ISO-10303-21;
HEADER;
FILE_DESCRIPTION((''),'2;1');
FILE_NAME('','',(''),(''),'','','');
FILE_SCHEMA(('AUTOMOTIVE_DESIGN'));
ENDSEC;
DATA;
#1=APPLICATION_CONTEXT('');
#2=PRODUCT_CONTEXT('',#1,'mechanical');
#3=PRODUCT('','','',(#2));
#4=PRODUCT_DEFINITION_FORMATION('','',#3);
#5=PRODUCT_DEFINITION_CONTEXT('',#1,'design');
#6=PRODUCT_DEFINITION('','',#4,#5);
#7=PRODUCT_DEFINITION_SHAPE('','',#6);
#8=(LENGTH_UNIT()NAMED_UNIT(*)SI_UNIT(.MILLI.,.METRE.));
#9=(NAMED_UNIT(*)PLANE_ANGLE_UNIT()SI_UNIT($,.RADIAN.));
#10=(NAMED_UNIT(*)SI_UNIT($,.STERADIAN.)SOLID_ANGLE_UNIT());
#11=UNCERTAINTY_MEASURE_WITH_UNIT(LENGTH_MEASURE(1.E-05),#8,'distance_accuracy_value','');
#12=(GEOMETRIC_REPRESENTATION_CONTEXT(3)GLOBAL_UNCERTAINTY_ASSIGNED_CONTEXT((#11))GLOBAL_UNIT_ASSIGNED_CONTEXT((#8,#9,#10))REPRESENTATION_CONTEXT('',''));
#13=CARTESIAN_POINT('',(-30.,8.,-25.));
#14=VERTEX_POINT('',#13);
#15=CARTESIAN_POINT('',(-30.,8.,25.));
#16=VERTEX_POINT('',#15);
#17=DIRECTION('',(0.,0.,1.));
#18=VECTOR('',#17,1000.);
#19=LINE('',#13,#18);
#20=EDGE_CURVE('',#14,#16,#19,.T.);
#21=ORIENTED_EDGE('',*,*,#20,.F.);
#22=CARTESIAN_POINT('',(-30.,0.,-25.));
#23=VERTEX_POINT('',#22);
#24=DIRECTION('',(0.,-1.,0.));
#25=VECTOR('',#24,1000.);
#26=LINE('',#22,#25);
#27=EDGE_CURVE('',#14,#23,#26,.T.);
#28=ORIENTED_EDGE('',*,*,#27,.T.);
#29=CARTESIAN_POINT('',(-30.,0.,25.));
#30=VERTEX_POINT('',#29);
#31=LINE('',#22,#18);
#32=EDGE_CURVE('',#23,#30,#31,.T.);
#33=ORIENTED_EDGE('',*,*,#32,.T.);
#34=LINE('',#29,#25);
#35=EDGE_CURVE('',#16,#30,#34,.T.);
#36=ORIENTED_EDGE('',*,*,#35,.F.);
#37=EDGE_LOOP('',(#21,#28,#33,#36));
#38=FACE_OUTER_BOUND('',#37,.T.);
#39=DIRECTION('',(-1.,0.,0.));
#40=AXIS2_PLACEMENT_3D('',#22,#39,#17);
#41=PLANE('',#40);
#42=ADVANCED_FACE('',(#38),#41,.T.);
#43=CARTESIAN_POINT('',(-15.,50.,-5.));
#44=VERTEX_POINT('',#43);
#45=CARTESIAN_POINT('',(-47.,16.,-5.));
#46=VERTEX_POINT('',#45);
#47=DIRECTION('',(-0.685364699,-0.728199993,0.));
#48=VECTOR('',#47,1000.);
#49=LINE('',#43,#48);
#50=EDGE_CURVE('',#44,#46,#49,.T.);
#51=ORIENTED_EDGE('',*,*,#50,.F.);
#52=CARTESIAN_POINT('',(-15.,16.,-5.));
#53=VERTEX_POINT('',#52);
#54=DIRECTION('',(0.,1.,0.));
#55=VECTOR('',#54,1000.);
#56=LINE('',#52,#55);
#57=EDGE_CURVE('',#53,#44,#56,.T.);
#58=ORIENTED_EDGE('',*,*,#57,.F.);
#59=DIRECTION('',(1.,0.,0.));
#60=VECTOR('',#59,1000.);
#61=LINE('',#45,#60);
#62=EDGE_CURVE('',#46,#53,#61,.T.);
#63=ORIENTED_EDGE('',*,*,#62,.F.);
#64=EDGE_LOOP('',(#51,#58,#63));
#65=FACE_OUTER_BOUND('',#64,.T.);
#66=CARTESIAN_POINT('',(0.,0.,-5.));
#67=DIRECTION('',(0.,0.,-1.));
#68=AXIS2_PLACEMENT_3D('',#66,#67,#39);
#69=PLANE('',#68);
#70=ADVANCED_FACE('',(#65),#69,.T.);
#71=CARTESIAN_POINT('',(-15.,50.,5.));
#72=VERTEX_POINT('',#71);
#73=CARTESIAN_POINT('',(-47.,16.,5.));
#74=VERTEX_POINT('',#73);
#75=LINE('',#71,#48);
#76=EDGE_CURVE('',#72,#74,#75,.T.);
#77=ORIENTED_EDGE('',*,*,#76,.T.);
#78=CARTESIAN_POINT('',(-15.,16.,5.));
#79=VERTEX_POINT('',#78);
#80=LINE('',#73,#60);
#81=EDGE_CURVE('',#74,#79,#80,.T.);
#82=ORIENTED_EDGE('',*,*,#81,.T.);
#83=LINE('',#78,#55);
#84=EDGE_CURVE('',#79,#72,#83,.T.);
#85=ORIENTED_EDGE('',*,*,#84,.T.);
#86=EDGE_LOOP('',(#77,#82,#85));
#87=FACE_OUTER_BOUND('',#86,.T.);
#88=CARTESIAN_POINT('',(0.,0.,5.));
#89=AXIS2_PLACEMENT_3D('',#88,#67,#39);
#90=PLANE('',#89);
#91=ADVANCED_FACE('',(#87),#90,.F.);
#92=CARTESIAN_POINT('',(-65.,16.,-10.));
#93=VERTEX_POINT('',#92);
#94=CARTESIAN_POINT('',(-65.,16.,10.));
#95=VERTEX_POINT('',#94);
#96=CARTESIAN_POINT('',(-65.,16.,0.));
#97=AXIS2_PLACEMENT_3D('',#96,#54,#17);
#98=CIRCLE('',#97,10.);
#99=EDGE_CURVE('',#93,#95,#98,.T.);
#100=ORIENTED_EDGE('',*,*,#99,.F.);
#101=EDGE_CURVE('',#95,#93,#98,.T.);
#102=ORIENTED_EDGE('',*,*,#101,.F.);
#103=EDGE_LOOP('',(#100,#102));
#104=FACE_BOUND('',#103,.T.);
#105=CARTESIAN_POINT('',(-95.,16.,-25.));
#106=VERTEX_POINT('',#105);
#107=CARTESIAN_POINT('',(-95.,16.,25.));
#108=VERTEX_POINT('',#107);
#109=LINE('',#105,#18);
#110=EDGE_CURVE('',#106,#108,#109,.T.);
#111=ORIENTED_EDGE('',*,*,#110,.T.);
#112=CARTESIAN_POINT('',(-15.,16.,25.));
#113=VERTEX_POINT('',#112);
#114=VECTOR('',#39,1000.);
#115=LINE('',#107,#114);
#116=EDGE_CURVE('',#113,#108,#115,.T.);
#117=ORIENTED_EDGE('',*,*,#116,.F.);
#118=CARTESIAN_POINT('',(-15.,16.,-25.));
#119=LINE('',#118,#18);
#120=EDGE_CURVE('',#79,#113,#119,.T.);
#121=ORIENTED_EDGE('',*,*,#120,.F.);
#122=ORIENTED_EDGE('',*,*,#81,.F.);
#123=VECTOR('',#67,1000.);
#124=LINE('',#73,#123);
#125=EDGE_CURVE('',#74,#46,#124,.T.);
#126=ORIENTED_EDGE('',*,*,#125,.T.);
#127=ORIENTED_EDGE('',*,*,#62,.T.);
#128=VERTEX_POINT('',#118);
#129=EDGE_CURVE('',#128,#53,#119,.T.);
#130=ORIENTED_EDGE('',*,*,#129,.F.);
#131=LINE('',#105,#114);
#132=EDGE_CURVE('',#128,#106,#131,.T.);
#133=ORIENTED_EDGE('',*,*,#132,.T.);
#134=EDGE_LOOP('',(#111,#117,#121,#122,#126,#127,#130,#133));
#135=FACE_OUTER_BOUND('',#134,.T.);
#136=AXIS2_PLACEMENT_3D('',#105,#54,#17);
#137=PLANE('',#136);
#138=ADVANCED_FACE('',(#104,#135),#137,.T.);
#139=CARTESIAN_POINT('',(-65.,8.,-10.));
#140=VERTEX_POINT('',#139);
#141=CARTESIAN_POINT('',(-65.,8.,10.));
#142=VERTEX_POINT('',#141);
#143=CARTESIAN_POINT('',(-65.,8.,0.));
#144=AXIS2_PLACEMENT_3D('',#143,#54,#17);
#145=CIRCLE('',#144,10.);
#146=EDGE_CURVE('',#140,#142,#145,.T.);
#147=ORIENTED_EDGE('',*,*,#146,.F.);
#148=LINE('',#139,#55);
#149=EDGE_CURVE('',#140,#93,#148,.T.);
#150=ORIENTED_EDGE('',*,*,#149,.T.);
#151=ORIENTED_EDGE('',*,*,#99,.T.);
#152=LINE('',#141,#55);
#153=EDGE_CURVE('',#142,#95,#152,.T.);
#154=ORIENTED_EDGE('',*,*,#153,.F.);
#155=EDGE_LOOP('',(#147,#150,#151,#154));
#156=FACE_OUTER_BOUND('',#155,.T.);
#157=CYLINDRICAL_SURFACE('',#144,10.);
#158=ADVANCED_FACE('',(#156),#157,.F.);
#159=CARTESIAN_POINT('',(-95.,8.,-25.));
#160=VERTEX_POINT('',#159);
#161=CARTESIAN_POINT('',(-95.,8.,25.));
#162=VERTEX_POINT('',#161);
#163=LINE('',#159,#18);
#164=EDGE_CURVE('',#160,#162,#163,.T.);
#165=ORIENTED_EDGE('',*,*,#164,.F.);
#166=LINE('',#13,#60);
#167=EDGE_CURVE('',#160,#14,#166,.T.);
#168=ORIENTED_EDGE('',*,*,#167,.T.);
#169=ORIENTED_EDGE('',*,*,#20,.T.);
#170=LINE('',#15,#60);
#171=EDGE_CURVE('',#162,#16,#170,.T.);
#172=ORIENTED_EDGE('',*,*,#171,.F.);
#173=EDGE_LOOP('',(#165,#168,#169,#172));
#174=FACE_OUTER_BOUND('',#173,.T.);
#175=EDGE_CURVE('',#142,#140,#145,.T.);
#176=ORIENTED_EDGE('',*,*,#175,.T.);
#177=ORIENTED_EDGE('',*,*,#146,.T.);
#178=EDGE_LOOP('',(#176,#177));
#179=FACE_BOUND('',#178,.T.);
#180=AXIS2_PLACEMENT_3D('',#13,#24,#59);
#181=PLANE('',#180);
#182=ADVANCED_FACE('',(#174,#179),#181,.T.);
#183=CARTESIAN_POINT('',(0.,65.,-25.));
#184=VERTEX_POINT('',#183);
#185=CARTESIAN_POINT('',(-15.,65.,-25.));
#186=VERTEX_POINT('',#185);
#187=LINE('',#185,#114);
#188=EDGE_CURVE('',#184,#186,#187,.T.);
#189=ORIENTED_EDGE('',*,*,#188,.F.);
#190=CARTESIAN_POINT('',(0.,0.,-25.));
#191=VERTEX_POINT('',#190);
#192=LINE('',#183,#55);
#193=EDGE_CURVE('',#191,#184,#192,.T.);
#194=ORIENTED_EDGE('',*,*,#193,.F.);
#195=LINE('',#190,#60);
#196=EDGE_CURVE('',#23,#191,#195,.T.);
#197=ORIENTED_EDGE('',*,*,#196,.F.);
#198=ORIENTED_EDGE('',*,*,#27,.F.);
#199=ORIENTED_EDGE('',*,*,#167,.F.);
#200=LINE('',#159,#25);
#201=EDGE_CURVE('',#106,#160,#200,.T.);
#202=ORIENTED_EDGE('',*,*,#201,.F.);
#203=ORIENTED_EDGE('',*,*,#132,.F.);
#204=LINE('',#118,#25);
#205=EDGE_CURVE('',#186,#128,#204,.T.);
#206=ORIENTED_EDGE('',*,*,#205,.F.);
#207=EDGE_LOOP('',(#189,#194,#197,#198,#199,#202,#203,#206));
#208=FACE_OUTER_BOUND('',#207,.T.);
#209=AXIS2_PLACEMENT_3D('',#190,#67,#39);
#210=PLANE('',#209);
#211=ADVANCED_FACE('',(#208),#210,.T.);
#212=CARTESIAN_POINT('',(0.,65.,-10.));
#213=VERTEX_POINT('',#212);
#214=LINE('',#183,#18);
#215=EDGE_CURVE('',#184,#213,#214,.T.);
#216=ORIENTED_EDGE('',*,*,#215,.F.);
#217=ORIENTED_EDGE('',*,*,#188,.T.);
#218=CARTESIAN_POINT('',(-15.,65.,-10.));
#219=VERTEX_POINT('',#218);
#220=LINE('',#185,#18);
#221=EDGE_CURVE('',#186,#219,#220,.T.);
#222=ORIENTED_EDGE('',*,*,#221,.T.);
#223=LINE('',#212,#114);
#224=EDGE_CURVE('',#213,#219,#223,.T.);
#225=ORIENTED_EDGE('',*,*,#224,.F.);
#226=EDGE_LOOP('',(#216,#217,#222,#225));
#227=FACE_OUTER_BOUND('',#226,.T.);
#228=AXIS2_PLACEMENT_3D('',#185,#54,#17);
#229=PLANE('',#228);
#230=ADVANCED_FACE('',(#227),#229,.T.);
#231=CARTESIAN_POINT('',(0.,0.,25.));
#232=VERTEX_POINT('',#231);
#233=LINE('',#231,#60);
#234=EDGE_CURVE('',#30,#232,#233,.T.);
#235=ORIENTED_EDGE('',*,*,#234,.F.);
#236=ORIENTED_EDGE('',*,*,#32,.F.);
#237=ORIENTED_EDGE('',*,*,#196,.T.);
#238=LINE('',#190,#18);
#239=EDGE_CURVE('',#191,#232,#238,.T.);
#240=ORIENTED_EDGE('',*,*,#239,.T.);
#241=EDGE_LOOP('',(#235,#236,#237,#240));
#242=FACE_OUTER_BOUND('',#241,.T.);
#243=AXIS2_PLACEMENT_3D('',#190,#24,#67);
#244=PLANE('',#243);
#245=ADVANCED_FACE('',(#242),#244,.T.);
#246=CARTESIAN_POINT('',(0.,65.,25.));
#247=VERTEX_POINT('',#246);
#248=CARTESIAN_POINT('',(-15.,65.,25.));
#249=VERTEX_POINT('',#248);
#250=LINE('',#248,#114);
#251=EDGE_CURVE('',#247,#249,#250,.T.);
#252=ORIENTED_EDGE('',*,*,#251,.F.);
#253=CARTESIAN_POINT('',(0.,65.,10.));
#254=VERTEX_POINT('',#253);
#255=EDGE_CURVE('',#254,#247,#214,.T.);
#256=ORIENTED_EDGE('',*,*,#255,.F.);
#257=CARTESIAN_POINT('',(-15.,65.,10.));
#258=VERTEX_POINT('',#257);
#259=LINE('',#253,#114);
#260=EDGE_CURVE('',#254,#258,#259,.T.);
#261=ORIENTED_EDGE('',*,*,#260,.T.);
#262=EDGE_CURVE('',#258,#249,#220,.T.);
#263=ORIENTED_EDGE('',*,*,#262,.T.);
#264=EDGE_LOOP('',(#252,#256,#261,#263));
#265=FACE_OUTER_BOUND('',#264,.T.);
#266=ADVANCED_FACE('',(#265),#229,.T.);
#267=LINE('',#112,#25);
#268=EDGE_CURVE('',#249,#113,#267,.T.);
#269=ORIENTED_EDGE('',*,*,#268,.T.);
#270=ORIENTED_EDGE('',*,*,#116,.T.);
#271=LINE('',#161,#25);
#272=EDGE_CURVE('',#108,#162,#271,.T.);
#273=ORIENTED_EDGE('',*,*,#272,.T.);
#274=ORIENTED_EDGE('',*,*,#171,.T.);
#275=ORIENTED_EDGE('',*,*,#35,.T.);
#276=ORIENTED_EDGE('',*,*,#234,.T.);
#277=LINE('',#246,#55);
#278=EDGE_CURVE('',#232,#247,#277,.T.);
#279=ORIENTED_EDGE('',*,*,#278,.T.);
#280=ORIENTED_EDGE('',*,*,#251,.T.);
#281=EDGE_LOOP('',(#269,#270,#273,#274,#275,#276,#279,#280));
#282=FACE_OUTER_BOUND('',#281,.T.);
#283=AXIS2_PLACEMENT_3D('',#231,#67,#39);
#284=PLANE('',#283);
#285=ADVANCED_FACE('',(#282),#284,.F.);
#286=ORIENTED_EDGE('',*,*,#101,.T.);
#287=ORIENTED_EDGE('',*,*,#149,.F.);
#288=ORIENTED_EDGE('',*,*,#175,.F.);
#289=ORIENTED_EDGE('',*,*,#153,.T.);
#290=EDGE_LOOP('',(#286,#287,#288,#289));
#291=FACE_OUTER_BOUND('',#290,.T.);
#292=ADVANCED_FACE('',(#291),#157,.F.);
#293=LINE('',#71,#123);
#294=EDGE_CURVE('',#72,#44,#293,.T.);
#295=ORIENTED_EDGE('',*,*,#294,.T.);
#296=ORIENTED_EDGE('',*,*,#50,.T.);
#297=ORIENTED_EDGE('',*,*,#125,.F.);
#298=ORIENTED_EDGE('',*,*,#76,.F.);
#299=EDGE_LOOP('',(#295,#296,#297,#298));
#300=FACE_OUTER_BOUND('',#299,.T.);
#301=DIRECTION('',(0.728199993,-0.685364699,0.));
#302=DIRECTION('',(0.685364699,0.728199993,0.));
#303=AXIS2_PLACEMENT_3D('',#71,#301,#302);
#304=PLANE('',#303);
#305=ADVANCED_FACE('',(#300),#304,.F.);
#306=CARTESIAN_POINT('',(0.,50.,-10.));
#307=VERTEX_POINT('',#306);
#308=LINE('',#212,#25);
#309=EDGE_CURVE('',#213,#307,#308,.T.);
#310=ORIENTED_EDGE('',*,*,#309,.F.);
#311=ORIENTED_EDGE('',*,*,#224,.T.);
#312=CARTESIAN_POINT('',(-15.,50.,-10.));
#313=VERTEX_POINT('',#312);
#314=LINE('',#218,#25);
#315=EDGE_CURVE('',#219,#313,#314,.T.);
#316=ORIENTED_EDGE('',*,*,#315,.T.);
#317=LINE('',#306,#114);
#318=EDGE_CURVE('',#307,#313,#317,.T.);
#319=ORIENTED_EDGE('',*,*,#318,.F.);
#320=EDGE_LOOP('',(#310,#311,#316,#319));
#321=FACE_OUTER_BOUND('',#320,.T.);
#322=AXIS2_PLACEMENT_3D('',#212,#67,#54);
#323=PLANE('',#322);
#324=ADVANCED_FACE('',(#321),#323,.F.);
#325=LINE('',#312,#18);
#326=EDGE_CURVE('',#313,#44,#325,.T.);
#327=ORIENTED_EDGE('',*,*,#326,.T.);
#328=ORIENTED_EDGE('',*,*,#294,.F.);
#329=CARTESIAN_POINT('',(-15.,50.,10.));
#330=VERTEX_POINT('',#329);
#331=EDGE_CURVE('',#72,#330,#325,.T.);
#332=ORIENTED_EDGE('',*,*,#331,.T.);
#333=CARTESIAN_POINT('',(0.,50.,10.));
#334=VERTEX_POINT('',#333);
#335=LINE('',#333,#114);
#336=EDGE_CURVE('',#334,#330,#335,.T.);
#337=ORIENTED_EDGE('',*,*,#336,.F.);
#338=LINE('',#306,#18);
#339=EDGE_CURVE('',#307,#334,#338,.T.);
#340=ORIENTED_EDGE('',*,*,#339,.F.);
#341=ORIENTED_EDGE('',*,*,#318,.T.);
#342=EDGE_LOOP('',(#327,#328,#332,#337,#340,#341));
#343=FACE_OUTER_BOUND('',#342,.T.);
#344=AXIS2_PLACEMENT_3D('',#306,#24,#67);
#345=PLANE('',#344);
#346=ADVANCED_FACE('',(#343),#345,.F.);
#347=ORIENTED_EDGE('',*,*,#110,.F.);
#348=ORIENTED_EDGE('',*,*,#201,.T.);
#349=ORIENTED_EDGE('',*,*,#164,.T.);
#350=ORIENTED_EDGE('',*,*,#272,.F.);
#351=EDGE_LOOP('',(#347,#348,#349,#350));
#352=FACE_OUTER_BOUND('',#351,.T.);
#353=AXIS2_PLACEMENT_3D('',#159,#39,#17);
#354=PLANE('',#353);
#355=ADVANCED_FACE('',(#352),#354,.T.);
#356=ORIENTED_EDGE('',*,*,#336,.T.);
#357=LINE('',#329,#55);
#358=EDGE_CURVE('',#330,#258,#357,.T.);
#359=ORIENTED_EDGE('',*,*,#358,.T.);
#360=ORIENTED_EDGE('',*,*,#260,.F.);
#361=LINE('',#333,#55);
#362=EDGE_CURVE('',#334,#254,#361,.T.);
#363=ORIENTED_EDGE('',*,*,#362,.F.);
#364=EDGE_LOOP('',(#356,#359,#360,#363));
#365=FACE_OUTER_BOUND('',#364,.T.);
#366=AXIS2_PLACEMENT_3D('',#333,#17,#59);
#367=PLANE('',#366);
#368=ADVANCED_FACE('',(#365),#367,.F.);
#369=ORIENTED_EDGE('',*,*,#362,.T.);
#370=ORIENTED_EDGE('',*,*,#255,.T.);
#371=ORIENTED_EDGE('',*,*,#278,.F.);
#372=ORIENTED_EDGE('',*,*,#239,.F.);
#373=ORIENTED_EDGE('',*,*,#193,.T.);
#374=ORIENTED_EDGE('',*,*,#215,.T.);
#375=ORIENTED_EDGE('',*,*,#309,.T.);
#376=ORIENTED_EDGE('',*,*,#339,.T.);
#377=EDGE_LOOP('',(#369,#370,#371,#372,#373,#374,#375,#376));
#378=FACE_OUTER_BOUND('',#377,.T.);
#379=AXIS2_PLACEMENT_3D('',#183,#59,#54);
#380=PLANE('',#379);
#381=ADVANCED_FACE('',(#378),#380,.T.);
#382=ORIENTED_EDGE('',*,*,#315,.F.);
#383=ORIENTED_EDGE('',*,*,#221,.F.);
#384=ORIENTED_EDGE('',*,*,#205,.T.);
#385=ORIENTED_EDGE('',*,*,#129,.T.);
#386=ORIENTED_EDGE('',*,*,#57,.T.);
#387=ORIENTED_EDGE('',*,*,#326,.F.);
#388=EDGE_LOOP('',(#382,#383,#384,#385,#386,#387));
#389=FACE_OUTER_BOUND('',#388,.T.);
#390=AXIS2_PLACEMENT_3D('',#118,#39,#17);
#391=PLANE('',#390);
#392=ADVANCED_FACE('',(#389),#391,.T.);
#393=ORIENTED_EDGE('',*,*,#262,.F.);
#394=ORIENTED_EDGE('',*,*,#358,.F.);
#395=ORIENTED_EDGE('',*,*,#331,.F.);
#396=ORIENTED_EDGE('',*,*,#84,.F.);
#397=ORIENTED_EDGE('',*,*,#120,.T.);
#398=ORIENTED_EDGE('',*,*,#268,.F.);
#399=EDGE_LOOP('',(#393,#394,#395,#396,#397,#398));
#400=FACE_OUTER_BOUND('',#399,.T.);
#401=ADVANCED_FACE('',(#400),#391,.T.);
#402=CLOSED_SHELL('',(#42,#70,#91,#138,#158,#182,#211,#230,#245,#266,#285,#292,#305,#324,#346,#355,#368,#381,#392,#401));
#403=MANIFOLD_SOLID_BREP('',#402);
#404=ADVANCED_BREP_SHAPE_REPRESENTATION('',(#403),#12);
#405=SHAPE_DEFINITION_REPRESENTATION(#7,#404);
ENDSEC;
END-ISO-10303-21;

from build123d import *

# Parameters (mm, degrees)
ANGLE_BRACKET_BODY_DEPTH      = 25
ANGLE_BRACKET_BODY_DEPTH_BACK = 25
TOP_SLOT_SKETCH_W             = 20
TOP_SLOT_SKETCH_H             = 15
TOP_SLOT_DEPTH                = 15
MOUNTING_HOLE_SKETCH_R        = 10
BASE_MOUNTING_HOLE_DEPTH      = 8
GUSSET_RIB_DEPTH              = 5


with BuildPart() as part:
    # Bracket L-Profile Sketch → Angle Bracket Body (new, two sides: drawn at the far end of the back side and taken through both)
    with BuildSketch(Plane.XY.offset(-ANGLE_BRACKET_BODY_DEPTH_BACK)):
        Polygon((0, 0), (-30, 0), (-30, 8), (-95, 8), (-95, 16), (-15, 16), (-15, 65), (0, 65), align=None)
    extrude(amount=ANGLE_BRACKET_BODY_DEPTH + ANGLE_BRACKET_BODY_DEPTH_BACK)

    # Top Slot Sketch → Top Slot (cut)
    with BuildSketch(Plane.ZY.offset(15)):
        with Locations((0, 57.5)):
            Rectangle(TOP_SLOT_SKETCH_W, TOP_SLOT_SKETCH_H)
    extrude(amount=-TOP_SLOT_DEPTH, mode=Mode.SUBTRACT)

    # Mounting Hole Sketch → Base Mounting Hole (cut)
    with BuildSketch(Plane(origin=(0, 16, 0), x_dir=(1, 0, 0), z_dir=(0, 1, 0))):
        with Locations(Location((-65, 0, 0), (0, 0, 270))):
            Circle(MOUNTING_HOLE_SKETCH_R)
    extrude(amount=-BASE_MOUNTING_HOLE_DEPTH, mode=Mode.SUBTRACT)

    # Gusset Sketch → Gusset Rib (add, symmetric)
    with BuildSketch(Plane.XY):
        Polygon((-15, 50), (-47, 16), (-15, 16), align=None)
    extrude(amount=GUSSET_RIB_DEPTH, both=True)


solid = part.part
